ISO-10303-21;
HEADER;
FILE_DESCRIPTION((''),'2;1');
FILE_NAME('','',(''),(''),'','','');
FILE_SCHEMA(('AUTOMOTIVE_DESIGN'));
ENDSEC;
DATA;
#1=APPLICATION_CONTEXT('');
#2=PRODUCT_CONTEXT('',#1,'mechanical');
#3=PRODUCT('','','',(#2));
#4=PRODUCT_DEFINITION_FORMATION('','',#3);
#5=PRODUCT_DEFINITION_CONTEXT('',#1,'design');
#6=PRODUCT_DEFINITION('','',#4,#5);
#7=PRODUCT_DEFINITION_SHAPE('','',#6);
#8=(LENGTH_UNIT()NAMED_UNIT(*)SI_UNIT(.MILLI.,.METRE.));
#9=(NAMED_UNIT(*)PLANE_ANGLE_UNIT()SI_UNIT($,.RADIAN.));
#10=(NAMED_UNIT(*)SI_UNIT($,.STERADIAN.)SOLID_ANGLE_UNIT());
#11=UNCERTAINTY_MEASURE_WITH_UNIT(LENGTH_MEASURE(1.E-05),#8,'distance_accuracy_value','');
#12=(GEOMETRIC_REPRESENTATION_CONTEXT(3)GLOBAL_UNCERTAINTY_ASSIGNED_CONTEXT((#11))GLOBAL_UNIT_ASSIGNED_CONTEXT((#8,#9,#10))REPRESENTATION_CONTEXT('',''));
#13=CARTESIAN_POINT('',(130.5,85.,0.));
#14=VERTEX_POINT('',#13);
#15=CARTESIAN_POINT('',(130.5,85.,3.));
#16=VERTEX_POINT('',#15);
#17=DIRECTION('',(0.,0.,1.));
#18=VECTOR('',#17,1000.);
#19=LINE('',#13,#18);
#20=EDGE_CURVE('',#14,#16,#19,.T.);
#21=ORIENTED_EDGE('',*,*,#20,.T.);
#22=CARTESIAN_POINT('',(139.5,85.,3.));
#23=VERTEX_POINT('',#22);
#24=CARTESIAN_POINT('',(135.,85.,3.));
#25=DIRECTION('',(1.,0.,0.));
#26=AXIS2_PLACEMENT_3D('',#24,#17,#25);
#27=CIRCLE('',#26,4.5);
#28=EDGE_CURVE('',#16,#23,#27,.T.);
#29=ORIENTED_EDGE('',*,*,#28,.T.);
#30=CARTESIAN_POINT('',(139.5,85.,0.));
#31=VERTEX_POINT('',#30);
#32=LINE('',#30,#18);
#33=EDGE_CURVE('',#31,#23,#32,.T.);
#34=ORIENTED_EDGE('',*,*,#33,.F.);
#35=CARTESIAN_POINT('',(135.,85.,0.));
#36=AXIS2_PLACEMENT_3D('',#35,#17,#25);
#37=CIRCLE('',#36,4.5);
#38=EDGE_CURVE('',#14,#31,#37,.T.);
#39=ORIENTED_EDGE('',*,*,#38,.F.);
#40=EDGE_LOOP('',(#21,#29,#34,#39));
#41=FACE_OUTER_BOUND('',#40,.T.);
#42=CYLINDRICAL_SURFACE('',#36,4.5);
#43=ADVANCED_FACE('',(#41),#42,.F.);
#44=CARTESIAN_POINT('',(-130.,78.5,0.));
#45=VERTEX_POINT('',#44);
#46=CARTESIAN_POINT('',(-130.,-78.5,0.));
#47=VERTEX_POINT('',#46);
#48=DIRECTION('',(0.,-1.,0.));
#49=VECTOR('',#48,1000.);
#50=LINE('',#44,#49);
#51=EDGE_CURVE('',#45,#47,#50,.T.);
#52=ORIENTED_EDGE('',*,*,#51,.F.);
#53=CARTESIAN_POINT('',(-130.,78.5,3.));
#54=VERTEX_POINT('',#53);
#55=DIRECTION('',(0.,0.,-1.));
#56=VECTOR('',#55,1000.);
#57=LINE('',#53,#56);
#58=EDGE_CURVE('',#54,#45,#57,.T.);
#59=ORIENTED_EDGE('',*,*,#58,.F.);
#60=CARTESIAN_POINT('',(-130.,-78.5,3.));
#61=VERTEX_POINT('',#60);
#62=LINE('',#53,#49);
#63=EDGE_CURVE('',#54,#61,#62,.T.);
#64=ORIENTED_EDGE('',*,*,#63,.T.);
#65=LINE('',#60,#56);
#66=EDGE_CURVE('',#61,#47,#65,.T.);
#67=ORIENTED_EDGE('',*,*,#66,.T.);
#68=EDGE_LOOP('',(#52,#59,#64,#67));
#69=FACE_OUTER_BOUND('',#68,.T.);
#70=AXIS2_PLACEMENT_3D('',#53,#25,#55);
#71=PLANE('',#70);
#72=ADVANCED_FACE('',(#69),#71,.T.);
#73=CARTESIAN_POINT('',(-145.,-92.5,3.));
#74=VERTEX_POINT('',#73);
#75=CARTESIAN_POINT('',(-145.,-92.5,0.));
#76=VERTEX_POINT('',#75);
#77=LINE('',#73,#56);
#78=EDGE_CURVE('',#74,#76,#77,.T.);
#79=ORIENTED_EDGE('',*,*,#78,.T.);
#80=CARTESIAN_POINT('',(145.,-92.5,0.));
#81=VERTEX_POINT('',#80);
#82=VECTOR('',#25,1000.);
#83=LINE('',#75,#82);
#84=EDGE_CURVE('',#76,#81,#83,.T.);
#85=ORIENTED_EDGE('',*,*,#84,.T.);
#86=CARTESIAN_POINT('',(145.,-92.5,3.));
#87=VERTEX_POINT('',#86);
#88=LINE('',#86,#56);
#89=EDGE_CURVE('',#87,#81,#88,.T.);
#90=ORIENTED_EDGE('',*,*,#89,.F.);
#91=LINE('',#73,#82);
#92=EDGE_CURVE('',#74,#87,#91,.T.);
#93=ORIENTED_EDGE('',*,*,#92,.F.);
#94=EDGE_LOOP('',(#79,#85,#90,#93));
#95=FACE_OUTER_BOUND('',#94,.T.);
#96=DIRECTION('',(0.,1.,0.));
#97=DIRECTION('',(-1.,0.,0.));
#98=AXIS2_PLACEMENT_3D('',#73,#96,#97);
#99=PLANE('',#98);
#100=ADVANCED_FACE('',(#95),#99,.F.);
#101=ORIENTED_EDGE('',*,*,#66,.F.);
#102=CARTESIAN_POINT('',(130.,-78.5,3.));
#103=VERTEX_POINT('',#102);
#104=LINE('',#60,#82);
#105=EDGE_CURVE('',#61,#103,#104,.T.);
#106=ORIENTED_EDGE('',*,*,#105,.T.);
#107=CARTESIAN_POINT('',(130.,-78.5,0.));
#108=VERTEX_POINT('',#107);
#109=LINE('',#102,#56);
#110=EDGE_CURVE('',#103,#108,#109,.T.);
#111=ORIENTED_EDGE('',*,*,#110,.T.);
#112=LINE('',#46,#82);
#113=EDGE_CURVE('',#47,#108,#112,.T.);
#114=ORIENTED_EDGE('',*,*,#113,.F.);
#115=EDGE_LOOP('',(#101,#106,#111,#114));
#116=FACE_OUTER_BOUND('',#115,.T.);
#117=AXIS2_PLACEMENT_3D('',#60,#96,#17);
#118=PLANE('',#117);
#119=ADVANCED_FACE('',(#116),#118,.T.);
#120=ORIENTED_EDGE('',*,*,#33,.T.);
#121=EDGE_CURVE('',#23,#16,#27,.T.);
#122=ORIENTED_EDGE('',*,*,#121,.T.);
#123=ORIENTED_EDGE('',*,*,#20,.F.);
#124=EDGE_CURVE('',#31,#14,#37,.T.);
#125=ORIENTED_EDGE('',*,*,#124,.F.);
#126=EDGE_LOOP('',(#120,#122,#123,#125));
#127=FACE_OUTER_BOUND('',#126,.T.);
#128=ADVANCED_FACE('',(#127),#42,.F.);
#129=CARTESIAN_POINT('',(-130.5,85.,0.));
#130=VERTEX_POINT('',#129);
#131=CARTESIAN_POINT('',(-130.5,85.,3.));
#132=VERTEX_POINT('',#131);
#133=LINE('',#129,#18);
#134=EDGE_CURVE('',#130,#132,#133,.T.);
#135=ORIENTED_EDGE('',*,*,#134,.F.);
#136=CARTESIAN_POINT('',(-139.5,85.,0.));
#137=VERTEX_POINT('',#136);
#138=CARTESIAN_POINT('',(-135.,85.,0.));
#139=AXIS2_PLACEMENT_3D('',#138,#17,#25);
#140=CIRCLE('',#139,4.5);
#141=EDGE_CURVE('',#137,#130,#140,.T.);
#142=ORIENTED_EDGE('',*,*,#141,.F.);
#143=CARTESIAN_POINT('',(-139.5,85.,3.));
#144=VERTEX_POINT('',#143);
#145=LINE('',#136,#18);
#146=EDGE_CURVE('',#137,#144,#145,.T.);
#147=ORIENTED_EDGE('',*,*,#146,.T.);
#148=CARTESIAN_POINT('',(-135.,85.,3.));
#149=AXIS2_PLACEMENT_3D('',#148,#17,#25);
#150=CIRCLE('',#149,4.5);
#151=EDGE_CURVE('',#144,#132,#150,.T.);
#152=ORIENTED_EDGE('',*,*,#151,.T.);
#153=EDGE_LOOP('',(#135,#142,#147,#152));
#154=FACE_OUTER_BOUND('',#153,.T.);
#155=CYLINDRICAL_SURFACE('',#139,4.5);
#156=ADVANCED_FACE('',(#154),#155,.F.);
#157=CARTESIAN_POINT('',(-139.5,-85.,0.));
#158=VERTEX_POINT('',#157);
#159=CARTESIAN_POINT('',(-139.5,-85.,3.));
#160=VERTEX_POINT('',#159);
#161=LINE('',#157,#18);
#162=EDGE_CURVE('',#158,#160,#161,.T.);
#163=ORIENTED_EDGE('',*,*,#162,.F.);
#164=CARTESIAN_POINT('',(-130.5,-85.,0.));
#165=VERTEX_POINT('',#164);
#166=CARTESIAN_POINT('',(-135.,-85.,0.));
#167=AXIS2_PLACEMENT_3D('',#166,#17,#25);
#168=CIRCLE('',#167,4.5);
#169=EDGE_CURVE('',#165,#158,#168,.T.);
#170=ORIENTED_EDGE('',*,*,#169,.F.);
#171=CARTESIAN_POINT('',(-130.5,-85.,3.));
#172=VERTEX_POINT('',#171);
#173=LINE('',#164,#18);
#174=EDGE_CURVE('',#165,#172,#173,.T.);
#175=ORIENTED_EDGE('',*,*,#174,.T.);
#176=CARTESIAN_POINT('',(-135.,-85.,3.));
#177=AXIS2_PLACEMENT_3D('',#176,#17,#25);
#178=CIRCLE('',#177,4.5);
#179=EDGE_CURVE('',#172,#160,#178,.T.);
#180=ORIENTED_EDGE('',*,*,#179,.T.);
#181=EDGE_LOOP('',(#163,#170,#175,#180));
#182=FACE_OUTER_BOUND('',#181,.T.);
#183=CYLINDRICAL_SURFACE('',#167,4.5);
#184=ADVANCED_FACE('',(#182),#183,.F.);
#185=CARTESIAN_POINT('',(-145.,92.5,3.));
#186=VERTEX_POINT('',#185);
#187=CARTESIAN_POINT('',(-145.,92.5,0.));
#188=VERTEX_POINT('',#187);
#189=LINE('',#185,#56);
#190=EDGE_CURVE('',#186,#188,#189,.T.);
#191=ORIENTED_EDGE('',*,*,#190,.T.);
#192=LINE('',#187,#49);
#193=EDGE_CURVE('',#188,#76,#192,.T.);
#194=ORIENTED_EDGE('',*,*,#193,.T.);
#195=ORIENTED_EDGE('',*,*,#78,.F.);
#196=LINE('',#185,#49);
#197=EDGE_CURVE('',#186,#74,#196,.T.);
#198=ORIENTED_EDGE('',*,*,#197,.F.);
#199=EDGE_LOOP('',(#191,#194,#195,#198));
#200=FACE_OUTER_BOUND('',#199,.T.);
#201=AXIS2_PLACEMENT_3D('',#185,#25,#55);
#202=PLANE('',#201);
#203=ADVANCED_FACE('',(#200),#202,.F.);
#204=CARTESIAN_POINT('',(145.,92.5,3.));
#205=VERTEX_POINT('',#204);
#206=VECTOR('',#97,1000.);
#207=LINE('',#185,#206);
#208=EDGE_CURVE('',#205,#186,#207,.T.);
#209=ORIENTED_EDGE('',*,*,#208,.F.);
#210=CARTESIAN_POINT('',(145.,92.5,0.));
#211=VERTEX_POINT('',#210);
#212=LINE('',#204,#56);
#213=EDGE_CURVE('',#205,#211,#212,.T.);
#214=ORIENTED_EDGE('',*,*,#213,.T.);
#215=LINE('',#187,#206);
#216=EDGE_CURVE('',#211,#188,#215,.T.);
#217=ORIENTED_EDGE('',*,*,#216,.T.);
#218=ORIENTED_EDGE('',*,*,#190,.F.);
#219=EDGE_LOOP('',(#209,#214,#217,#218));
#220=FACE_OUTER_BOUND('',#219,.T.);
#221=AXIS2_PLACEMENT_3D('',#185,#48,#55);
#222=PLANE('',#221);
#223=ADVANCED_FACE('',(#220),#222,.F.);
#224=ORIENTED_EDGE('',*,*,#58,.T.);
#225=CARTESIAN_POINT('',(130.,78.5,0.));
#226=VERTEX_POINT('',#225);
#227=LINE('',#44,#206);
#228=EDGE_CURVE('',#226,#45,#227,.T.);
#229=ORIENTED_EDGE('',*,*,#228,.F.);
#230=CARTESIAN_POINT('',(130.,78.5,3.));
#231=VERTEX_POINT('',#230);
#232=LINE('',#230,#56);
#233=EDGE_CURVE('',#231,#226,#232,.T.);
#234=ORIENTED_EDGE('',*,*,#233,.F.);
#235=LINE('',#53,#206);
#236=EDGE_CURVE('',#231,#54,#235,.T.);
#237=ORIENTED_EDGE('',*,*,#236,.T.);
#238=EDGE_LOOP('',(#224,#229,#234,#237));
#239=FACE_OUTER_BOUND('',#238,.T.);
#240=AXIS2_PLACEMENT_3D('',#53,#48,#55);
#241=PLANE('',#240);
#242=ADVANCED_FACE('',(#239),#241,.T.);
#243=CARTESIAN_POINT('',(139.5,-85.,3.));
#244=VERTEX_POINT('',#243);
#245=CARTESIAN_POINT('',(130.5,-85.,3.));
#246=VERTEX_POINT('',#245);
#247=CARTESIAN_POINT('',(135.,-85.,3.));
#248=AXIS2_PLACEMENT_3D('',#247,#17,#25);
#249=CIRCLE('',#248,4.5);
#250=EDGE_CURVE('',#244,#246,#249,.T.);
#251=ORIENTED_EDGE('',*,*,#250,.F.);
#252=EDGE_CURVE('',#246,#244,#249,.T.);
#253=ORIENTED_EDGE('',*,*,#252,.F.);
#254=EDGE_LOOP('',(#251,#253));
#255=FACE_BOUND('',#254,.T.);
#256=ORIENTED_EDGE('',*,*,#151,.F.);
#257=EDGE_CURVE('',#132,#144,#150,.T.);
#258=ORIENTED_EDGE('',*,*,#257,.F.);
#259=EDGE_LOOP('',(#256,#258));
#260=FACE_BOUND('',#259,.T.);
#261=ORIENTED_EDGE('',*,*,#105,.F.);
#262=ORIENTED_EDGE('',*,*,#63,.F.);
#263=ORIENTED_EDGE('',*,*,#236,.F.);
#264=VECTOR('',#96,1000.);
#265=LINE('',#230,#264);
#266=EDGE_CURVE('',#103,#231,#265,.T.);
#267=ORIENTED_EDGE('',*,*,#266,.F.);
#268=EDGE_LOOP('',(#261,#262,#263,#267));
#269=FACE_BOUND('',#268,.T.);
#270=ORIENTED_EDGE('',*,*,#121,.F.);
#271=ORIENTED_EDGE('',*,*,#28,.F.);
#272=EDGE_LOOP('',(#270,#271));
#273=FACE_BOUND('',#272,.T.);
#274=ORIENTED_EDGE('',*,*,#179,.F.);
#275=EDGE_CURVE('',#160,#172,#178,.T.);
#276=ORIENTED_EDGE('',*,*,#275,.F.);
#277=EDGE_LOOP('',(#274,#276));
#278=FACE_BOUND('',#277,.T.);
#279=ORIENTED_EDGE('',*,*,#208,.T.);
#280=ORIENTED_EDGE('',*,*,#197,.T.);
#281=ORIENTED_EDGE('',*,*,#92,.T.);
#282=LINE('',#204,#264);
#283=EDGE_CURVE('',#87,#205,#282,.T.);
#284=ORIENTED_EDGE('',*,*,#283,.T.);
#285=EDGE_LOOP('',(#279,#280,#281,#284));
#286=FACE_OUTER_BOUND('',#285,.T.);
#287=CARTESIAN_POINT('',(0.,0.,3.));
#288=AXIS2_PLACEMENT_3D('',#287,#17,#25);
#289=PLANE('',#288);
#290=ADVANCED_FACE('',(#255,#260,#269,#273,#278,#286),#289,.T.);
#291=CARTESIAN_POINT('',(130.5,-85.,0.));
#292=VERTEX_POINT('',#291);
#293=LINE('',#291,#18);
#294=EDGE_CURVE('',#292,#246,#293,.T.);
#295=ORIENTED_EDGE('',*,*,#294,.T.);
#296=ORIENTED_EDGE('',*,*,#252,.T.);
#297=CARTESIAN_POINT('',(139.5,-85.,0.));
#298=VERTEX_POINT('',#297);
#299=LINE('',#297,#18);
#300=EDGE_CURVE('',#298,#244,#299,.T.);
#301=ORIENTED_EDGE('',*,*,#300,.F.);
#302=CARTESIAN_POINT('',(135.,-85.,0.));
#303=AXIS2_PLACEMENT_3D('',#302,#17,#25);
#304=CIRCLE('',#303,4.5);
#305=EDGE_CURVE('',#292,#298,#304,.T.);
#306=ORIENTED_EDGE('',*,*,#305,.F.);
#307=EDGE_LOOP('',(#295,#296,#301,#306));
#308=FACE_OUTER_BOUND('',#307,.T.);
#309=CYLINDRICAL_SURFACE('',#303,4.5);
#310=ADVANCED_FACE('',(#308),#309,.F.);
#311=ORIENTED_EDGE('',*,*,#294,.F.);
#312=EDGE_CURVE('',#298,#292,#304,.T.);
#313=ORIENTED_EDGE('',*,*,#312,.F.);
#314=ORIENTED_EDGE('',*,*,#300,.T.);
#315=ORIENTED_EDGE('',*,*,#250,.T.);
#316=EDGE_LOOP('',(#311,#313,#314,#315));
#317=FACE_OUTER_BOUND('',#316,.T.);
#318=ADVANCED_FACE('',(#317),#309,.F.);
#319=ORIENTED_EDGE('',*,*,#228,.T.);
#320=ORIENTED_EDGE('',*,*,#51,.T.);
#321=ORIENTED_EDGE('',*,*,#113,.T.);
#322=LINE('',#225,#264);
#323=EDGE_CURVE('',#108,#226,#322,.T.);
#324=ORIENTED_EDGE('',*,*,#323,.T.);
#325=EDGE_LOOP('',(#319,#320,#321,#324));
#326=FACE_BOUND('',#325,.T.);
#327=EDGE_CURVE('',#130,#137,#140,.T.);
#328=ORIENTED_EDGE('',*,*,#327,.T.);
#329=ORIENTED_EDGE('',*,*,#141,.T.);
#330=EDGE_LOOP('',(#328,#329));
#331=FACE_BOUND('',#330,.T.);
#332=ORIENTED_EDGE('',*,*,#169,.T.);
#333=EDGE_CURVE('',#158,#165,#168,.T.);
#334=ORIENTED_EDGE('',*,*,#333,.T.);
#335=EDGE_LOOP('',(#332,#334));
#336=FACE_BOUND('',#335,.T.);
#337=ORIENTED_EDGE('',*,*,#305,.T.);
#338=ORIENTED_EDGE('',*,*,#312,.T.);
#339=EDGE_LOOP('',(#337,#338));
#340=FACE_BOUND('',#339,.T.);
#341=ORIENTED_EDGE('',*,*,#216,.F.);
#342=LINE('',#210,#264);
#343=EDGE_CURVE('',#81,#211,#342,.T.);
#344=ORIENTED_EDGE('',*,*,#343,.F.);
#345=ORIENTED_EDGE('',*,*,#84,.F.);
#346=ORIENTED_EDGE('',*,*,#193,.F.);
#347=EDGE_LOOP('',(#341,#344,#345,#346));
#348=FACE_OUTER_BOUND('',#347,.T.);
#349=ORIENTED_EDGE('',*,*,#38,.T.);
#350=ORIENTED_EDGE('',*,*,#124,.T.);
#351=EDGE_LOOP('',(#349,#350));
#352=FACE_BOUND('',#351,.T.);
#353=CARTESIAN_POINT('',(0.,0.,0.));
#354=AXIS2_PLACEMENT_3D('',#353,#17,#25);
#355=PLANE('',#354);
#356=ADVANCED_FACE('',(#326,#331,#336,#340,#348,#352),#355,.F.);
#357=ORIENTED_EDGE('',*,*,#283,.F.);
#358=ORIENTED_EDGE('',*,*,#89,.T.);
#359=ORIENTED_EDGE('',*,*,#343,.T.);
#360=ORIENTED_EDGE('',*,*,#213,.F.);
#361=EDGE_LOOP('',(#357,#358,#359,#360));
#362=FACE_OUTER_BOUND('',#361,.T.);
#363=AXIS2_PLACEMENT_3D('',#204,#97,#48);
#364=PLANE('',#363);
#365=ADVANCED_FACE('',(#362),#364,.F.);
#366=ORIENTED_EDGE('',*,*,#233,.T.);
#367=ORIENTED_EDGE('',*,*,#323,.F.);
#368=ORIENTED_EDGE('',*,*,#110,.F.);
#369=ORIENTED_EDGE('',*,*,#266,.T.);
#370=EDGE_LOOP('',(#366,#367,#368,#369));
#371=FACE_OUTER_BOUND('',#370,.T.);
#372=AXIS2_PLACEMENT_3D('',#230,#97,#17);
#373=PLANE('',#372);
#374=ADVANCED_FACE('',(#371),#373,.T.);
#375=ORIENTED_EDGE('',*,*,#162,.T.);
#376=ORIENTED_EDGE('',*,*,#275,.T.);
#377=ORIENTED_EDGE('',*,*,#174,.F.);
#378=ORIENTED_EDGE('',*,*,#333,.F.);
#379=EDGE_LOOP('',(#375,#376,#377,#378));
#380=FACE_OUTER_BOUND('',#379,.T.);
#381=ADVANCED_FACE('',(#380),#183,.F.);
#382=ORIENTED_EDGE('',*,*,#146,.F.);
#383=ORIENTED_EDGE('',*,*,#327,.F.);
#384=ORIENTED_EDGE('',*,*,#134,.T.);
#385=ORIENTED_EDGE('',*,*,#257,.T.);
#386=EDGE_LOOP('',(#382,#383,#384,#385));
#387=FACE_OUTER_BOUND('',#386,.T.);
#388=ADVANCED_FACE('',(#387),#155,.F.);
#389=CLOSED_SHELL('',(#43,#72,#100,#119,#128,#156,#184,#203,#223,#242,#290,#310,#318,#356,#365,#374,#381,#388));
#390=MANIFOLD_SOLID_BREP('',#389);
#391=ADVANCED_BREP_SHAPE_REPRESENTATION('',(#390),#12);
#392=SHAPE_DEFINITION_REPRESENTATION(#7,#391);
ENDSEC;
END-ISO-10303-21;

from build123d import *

# Parameters (mm, degrees)
SKETCH1_W            = 290
SKETCH1_H            = 185
SKETCH1_W_2          = 260
SKETCH1_H_2          = 157
BOSS_EXTRUDE1_DEPTH  = 3
SKETCH2_R            = 4.5
CUT_EXTRUDE1_DEPTH   = 3
LPATTERN1_COUNT      = 2
LPATTERN1_PITCH      = 270
LPATTERN1_COUNT_DIR2 = 2
LPATTERN1_PITCH_DIR2 = 170


with BuildPart() as part:
    # Sketch1 → Boss-Extrude1 (new body)
    with BuildSketch(Plane.XY):
        Rectangle(SKETCH1_W, SKETCH1_H)
        Rectangle(SKETCH1_W_2, SKETCH1_H_2, mode=Mode.SUBTRACT)
    extrude(amount=BOSS_EXTRUDE1_DEPTH)

    # Sketch2 → Cut-Extrude1 (cut)
    with BuildSketch(Plane.XY.offset(3)):
        with Locations((-135, 85)):
            Circle(SKETCH2_R)
    cut_extrude1 = extrude(amount=-CUT_EXTRUDE1_DEPTH, mode=Mode.SUBTRACT)

    # LPattern1: Cut-Extrude1 2 × 2
    with Locations(*[(i * LPATTERN1_PITCH, -j * LPATTERN1_PITCH_DIR2, 0) for i in range(LPATTERN1_COUNT) for j in range(LPATTERN1_COUNT_DIR2) if (i, j) != (0, 0)]):
        add(cut_extrude1, mode=Mode.SUBTRACT)


solid = part.part
